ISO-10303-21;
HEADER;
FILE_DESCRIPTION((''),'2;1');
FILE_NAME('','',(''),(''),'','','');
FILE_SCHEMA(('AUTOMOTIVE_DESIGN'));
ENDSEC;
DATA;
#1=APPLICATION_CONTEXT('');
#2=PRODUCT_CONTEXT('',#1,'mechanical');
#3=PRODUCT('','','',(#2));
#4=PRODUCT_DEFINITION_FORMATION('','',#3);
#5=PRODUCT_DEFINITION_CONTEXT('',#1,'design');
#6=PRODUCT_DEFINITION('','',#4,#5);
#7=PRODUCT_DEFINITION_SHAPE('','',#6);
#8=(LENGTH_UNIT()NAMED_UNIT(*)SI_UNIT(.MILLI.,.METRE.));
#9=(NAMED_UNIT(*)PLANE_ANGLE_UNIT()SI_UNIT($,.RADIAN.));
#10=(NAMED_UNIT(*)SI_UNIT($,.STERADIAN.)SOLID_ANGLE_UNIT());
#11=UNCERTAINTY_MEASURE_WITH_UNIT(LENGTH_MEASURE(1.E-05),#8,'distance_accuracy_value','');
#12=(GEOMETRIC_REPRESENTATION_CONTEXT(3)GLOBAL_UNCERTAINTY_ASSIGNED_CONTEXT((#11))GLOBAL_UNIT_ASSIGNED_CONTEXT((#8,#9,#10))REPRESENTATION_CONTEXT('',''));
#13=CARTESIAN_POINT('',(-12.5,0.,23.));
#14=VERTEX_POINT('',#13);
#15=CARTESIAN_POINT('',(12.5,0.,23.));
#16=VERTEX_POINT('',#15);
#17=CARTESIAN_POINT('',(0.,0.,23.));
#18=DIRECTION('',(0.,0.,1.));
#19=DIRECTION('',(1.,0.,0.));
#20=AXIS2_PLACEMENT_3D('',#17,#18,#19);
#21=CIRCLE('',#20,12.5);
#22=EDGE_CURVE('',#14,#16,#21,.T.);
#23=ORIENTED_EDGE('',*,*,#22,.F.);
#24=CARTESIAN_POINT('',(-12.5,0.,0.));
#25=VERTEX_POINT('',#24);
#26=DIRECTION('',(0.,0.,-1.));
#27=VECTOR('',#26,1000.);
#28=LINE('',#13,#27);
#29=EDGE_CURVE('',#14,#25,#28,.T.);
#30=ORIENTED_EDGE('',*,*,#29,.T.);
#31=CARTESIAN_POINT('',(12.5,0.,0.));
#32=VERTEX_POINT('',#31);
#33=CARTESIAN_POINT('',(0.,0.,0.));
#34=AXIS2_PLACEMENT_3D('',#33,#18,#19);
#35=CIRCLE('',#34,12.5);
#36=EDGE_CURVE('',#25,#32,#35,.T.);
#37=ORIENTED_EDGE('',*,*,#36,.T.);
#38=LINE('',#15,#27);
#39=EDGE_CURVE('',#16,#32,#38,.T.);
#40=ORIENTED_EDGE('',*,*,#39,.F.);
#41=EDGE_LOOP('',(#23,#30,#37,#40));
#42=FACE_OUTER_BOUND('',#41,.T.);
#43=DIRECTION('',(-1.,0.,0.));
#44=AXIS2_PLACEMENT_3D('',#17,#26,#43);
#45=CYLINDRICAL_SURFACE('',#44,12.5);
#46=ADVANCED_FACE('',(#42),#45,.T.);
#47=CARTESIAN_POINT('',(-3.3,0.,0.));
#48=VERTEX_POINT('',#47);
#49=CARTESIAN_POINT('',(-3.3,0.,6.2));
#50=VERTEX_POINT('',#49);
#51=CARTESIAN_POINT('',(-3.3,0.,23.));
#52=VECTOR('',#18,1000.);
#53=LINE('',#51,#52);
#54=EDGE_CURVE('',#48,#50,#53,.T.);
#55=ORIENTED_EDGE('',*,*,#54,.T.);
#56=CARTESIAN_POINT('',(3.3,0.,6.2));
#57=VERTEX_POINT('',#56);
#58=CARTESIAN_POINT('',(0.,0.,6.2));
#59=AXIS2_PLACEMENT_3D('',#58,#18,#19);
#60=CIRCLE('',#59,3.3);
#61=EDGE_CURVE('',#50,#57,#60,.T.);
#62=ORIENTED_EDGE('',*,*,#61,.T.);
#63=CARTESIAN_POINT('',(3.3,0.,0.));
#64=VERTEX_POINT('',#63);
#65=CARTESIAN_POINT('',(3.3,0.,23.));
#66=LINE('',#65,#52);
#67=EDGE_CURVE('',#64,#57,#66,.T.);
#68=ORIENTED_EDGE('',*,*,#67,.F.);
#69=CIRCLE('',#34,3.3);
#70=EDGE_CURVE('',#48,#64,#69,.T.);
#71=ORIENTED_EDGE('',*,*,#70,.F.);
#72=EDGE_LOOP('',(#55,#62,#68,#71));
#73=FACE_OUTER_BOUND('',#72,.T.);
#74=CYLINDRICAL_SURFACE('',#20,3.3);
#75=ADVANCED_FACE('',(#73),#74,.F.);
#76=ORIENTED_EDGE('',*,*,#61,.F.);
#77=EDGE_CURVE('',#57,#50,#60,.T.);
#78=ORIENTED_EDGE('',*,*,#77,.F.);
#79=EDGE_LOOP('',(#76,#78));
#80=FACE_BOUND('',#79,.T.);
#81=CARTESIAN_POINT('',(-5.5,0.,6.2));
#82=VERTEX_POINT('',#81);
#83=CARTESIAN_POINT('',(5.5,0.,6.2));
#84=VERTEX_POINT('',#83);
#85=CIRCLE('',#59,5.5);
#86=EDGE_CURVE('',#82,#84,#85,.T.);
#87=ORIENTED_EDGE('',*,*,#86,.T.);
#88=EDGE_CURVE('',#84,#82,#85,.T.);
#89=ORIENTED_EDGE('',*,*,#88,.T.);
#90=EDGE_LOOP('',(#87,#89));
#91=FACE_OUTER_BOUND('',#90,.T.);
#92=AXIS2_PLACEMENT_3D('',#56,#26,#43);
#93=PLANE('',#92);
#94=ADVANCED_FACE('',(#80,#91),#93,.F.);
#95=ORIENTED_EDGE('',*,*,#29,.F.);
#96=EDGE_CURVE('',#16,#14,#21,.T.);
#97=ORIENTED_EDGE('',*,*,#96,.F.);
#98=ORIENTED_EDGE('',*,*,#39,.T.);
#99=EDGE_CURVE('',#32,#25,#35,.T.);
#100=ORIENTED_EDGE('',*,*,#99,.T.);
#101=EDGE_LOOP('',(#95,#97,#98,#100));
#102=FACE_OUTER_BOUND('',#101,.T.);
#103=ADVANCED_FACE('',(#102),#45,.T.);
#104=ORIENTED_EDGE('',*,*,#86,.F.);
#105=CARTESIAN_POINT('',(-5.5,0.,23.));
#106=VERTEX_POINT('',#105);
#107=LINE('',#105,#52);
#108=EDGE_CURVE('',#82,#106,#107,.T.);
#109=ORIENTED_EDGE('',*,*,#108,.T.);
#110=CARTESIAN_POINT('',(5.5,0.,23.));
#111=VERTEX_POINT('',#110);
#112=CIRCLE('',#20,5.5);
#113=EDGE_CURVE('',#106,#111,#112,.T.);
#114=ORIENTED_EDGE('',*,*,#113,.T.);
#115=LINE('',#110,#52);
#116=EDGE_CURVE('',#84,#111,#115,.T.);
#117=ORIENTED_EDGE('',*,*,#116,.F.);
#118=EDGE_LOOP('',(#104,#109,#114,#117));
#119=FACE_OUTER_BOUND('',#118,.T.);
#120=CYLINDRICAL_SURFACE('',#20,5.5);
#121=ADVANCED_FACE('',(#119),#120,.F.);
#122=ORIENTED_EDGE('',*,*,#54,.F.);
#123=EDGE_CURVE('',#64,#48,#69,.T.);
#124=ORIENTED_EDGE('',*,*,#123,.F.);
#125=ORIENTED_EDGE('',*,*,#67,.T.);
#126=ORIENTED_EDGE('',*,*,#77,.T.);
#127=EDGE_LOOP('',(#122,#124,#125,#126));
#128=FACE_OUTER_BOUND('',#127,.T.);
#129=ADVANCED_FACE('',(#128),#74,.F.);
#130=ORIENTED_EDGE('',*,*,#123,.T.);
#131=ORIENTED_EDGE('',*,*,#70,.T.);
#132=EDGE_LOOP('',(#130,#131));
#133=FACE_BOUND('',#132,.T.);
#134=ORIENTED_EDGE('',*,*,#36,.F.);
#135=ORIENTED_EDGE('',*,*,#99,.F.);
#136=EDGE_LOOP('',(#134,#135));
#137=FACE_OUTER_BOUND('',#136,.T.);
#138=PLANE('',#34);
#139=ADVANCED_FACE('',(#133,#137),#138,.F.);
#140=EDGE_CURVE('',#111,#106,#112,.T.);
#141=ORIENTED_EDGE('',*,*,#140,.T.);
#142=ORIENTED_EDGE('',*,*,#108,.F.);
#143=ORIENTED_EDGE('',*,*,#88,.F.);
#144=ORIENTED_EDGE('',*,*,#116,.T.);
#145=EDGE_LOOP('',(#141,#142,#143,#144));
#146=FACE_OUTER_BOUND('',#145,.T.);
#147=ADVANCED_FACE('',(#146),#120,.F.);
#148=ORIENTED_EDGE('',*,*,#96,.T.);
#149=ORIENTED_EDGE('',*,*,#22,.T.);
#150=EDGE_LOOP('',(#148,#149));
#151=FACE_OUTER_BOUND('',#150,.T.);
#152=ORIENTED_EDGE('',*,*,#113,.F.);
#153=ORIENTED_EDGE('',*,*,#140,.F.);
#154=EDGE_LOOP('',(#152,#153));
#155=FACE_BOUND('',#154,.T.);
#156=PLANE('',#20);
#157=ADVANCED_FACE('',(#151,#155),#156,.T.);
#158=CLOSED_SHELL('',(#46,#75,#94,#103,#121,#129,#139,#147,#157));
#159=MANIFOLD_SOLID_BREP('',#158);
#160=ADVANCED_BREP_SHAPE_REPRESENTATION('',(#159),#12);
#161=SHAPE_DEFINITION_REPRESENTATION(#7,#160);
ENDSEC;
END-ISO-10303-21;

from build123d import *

# Parameters (mm, degrees)
SKETCH_1_R                   = 12.5
EXTRUDE_1_DEPTH              = 23
HOLE_WIZARD_M6_1_D           = 6.6
HOLE_WIZARD_M6_1_CBORE_D     = 11
HOLE_WIZARD_M6_1_CBORE_DEPTH = 16.8


with BuildPart() as part:
    # 草图1 → 凸台-拉伸1 (new body)
    with BuildSketch(Plane.XY):
        Circle(SKETCH_1_R)
    extrude(amount=EXTRUDE_1_DEPTH)

    # M6 六角圆柱头螺钉的柱形沉头孔1 (through all)
    with Locations(Plane.XY.offset(23)):
        with Locations((0, 0)):
            CounterBoreHole(HOLE_WIZARD_M6_1_D / 2, HOLE_WIZARD_M6_1_CBORE_D / 2, HOLE_WIZARD_M6_1_CBORE_DEPTH)


solid = part.part
